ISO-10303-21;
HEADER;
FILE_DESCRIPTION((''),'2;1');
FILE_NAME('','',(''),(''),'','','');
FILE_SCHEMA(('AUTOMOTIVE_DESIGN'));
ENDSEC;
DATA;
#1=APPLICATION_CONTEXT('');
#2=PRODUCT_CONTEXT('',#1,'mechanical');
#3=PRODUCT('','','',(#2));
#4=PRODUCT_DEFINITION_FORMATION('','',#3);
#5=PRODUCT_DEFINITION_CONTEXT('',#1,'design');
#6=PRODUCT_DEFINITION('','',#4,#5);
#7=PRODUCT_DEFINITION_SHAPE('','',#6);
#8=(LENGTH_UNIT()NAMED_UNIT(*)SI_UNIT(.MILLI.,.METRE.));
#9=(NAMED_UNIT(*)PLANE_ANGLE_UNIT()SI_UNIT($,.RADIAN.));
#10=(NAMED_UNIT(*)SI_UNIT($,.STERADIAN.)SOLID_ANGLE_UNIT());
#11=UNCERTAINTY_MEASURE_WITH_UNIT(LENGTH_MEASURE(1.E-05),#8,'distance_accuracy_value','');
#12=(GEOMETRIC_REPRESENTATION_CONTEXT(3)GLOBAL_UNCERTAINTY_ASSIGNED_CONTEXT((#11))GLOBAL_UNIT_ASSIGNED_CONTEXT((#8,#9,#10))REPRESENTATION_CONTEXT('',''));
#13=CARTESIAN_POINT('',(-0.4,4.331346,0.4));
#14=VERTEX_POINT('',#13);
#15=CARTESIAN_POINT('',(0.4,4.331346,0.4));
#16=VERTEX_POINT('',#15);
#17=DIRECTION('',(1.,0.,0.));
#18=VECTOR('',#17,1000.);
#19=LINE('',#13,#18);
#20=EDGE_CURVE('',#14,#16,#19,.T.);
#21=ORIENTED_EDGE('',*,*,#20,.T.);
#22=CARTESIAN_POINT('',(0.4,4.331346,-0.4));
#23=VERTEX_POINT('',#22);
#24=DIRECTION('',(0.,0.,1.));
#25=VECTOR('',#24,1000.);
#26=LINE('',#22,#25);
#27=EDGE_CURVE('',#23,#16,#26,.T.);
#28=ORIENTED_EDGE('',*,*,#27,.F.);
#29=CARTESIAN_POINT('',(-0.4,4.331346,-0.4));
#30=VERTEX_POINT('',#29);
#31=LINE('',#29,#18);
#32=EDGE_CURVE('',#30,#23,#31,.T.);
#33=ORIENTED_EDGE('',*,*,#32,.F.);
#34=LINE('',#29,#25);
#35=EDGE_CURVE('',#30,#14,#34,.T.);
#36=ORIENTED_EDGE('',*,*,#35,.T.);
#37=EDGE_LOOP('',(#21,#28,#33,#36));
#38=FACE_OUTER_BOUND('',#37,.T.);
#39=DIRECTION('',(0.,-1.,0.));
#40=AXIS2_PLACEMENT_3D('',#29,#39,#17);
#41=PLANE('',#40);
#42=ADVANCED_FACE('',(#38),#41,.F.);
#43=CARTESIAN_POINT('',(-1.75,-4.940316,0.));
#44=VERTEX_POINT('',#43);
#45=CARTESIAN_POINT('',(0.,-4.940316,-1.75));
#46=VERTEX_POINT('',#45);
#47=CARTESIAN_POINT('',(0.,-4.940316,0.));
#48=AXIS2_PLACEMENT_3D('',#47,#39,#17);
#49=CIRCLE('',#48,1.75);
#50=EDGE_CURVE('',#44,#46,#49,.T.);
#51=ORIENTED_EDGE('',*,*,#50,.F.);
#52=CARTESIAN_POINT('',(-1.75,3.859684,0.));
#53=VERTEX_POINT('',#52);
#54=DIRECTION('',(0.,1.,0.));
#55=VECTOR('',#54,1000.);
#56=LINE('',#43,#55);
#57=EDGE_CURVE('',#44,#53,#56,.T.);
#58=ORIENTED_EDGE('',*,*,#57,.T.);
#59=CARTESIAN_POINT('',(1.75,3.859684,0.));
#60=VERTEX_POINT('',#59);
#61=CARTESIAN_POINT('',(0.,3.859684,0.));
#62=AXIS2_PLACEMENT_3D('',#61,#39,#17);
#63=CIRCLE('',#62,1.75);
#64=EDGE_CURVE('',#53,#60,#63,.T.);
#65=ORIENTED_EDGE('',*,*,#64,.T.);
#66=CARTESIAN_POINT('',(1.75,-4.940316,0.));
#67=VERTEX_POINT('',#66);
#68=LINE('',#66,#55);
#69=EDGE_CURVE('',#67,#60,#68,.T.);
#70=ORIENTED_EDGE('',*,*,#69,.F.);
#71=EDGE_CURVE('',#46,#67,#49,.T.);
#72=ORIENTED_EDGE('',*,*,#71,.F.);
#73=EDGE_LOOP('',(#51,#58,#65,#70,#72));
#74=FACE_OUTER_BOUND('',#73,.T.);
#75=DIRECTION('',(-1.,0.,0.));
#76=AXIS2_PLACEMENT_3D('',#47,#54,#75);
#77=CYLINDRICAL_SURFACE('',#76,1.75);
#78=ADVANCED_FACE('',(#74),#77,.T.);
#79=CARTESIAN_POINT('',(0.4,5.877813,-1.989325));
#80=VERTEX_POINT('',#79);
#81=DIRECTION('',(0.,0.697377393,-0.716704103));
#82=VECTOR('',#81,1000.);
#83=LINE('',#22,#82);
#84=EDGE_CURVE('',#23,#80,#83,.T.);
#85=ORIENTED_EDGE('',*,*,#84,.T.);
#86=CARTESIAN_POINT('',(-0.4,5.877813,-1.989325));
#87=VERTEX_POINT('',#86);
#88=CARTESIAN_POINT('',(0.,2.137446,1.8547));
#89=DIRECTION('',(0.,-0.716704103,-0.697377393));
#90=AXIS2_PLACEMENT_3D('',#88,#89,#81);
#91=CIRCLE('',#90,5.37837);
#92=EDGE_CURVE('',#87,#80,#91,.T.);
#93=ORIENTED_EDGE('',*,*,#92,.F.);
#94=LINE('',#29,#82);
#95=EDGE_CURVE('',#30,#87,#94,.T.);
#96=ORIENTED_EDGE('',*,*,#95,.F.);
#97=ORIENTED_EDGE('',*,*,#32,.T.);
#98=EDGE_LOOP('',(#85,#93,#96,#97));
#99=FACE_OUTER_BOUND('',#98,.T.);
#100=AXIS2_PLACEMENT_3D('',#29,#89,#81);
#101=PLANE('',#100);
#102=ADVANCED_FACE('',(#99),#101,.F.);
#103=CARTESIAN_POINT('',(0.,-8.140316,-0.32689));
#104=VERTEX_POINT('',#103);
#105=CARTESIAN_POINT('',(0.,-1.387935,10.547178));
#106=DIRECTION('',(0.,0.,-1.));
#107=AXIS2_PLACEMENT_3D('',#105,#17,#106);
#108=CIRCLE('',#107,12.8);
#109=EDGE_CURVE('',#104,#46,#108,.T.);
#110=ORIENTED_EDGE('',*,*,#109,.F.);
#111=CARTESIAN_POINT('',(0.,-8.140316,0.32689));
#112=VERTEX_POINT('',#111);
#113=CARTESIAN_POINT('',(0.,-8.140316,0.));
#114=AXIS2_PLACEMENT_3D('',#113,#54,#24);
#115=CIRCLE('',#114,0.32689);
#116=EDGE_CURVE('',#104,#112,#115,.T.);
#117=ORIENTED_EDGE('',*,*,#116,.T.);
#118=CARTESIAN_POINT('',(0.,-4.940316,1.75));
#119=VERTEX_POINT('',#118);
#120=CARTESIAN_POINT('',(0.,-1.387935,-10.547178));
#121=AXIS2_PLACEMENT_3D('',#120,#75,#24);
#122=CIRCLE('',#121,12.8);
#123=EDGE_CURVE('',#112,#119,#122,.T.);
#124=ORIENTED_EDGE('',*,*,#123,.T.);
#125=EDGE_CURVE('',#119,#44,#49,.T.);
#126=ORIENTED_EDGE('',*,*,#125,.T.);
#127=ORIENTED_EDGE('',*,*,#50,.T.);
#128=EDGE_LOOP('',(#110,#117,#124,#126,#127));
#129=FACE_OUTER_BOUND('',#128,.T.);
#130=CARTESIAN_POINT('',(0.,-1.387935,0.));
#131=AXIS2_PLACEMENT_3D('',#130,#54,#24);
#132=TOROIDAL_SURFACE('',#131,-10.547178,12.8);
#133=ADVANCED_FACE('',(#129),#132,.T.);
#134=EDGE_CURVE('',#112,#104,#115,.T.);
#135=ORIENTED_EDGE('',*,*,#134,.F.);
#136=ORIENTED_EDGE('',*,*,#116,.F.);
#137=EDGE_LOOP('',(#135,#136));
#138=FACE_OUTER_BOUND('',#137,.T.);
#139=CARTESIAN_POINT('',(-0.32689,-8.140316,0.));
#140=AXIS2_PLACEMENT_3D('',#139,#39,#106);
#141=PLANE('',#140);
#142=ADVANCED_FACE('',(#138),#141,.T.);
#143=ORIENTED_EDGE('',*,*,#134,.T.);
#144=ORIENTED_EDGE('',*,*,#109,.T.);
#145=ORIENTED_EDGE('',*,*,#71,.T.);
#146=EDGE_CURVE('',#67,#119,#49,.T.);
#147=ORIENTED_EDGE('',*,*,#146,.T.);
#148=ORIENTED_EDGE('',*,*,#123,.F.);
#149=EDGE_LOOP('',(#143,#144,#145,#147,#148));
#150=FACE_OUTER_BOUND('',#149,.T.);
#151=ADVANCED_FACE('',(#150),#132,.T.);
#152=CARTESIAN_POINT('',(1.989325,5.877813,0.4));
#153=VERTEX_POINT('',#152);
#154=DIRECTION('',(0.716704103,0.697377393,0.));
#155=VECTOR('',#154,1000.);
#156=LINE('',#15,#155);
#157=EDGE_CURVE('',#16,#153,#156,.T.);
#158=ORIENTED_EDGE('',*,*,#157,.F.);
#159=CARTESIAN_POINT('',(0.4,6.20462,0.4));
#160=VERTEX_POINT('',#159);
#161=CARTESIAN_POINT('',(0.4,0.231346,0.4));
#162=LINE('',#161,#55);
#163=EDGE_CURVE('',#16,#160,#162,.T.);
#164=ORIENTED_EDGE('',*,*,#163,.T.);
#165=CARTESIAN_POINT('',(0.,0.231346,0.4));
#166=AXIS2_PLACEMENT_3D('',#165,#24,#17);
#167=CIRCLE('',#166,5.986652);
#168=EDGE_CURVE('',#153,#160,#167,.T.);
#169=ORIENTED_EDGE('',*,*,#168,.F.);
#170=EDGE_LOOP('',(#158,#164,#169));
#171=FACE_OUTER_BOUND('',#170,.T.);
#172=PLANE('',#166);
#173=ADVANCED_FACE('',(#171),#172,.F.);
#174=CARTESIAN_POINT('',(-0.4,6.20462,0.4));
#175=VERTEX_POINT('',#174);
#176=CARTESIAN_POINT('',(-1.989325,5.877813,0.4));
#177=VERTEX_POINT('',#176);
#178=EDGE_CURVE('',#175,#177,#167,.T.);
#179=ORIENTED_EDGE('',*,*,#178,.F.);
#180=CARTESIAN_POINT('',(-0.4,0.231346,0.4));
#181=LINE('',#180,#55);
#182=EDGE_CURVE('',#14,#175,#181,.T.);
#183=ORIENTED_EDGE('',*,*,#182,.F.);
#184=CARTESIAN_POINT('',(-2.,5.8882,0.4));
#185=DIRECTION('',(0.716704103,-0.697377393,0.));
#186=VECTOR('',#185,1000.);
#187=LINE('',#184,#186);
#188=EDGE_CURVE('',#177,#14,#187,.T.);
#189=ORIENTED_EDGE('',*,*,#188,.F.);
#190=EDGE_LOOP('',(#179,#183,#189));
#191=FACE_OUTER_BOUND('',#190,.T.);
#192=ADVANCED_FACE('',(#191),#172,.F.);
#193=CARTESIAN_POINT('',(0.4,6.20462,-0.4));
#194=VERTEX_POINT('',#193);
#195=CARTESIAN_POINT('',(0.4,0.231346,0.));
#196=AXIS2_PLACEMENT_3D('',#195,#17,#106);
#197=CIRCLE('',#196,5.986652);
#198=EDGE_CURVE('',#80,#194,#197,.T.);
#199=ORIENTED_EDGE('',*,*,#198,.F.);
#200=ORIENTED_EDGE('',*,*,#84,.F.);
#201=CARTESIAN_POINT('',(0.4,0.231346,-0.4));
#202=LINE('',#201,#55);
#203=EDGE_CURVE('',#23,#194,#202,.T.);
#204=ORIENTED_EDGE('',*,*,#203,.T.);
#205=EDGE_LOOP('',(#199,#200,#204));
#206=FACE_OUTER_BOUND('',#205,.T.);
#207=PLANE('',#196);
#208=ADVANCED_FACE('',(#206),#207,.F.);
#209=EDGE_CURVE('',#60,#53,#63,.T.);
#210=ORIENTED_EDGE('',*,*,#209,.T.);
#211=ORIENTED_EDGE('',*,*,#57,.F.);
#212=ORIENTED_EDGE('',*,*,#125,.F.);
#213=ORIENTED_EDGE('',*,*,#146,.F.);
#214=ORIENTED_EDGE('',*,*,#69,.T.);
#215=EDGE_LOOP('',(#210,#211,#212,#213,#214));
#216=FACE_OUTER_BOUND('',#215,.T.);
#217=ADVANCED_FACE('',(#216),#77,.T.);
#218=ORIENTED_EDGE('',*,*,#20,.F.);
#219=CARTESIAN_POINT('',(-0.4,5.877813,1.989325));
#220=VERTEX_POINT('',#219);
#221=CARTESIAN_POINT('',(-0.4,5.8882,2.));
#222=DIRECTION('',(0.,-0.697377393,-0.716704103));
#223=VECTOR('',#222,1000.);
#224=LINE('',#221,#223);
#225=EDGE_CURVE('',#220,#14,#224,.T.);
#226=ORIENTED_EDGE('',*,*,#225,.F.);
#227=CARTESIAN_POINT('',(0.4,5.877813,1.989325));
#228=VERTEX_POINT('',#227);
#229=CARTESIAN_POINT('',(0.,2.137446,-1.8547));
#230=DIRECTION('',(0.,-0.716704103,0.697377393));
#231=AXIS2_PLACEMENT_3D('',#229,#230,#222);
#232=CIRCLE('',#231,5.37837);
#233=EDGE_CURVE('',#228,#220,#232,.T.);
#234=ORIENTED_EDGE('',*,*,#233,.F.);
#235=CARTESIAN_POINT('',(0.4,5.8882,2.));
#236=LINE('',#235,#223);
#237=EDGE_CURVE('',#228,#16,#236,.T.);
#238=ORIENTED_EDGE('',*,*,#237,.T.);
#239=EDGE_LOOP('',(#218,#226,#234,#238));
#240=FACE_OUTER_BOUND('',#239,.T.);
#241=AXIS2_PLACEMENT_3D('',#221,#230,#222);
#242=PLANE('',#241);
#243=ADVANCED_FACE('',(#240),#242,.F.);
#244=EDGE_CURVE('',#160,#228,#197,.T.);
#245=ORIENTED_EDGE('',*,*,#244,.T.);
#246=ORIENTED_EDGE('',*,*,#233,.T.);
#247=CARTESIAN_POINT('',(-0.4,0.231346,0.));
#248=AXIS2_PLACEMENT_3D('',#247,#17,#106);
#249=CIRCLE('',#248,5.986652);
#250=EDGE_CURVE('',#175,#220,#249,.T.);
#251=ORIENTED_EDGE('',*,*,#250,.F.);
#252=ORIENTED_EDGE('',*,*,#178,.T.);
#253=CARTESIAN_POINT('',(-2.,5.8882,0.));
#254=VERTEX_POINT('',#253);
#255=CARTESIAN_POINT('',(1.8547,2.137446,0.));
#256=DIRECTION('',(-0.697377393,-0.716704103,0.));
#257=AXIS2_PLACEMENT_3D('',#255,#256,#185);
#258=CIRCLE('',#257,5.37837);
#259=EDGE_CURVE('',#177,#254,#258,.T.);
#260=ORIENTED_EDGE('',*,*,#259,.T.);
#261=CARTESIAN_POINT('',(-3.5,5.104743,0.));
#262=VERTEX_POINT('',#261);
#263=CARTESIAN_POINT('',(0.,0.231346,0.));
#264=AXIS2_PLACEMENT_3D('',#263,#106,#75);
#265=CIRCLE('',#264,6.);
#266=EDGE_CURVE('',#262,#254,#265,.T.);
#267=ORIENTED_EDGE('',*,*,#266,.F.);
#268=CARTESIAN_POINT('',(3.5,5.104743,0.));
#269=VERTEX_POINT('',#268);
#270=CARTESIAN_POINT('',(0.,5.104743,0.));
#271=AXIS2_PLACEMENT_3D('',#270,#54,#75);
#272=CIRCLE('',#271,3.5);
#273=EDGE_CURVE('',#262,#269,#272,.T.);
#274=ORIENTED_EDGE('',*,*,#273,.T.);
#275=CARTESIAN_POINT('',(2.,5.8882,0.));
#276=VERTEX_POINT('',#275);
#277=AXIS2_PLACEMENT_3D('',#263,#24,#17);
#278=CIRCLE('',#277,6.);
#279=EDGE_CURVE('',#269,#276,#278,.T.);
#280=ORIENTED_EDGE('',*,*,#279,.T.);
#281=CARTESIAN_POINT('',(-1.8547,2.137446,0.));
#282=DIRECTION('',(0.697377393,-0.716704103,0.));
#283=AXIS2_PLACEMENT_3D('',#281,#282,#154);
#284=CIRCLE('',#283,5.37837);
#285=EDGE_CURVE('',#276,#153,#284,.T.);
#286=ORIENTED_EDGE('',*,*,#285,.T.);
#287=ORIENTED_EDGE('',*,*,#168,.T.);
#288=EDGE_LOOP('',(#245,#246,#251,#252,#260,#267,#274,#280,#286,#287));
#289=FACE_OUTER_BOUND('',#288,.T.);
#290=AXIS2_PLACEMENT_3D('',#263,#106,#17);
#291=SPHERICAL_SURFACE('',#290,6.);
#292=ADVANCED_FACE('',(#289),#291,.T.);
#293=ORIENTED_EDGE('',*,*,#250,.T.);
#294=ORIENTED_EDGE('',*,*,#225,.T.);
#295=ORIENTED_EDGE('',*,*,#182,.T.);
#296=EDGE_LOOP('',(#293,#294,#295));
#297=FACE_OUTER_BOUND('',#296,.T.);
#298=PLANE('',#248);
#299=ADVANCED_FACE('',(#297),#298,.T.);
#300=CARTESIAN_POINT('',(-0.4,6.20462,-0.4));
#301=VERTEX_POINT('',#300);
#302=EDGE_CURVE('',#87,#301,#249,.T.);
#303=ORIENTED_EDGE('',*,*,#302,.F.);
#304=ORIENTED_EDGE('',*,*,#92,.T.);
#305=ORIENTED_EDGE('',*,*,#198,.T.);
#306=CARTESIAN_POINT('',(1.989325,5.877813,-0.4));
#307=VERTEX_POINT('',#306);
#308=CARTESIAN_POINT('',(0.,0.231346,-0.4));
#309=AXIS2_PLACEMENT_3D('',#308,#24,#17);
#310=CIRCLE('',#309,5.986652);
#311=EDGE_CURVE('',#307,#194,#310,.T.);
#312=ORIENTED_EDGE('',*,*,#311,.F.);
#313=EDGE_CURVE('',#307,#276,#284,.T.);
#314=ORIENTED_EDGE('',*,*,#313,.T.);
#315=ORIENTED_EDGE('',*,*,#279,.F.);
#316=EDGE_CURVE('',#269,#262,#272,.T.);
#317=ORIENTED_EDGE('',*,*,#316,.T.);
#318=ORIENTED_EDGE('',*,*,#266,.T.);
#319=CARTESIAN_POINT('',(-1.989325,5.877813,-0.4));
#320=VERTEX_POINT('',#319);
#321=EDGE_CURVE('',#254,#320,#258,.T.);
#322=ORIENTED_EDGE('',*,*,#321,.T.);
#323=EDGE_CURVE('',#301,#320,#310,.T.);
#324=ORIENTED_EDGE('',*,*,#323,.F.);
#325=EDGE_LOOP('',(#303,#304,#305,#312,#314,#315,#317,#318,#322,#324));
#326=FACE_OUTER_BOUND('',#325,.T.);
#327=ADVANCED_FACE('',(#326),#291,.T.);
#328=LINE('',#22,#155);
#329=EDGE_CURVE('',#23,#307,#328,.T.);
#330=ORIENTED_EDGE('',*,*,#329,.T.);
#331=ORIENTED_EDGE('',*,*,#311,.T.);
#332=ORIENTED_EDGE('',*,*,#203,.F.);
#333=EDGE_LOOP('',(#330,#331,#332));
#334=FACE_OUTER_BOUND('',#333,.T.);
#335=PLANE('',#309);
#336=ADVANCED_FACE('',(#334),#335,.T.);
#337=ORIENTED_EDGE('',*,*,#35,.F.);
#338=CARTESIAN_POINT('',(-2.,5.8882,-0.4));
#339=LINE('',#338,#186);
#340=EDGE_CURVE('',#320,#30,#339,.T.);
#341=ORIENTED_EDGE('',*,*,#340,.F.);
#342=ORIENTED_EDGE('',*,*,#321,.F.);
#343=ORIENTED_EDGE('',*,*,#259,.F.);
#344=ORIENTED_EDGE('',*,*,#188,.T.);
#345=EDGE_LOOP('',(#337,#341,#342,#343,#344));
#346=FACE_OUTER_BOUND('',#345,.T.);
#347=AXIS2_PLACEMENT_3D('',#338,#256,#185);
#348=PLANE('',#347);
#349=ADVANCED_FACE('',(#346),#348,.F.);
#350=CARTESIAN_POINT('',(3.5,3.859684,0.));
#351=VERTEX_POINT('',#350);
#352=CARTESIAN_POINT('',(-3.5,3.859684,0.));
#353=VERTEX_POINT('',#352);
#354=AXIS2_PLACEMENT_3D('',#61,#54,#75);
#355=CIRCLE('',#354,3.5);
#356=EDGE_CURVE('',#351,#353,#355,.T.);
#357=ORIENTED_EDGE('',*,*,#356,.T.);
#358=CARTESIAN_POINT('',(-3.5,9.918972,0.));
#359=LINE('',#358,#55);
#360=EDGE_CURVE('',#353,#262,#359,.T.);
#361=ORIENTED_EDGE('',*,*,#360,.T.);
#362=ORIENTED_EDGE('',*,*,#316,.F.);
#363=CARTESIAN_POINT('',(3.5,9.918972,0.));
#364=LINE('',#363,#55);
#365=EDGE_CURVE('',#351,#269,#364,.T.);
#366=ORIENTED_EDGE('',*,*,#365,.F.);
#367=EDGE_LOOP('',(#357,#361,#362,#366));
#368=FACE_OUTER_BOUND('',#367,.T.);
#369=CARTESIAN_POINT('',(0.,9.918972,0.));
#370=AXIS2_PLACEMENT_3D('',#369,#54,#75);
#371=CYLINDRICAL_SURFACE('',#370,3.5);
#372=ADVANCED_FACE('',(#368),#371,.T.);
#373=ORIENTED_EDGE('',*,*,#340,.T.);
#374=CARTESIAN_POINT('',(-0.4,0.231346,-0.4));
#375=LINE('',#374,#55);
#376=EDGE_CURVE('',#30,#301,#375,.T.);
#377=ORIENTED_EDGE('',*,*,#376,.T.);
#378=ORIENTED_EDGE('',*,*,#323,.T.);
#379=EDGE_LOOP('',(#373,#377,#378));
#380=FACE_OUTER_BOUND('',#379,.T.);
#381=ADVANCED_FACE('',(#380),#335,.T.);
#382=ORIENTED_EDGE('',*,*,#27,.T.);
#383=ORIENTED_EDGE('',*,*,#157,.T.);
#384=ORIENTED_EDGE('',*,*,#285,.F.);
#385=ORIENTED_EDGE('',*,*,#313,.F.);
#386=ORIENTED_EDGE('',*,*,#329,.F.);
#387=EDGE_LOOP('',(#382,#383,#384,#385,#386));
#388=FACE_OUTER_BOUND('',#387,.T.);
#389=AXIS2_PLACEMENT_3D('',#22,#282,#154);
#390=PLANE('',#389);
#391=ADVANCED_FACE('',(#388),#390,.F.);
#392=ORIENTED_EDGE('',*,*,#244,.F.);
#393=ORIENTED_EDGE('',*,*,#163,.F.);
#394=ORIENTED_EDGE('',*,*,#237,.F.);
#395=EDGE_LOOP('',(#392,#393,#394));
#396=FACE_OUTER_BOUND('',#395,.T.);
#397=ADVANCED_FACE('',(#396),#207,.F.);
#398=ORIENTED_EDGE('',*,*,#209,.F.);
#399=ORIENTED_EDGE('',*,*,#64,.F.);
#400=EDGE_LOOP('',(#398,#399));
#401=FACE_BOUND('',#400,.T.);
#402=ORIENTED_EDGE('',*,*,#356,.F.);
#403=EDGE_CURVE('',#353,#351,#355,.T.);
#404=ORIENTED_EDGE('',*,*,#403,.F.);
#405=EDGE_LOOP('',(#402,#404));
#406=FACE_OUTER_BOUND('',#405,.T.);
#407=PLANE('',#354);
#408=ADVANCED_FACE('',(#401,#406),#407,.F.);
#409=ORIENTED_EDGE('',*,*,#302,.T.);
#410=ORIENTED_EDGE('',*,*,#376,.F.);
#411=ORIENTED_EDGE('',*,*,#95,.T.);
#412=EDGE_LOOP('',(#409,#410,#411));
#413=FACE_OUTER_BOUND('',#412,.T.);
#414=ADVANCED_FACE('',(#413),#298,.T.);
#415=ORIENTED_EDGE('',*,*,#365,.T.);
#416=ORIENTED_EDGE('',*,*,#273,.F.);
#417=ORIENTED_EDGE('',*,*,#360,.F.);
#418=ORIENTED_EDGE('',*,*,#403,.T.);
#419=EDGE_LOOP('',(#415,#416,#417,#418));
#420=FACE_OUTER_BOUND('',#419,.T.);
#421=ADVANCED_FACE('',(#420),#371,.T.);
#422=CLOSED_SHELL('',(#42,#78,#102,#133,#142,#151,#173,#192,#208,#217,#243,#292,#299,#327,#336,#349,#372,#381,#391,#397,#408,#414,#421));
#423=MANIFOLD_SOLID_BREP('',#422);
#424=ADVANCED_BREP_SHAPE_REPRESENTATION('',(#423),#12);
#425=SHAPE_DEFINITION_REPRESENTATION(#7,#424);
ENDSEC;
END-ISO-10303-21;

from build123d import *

# Parameters (mm, degrees)
SKETCH2_R           = 1.75
BOSS_EXTRUDE1_DEPTH = 8.8
CUT_EXTRUDE1_DEPTH  = 0.4
CIRPATTERN1_COUNT   = 4


with BuildPart() as part:
    # Sketch1 → Revolve2 (revolve)
    with BuildSketch(Plane.XY, mode=Mode.PRIVATE) as revolve2_sk:
        with BuildLine():
            Line((0, 3.8596837944664038), (3.5000000000000013, 3.8596837944664038))
            Line((3.5000000000000013, 3.8596837944664038), (3.5000000000000013, 5.104743083003953))
            ThreePointArc((3.5000000000000013, 5.104743083003953), (1.8384255445316686, 5.9427548013385545), (8.7e-16, 6.231345910599472))
            Line((8.7e-16, 6.231345910599472), (0, 3.8596837944664038))
        make_face()
    revolve(revolve2_sk.sketch.rotate(Axis((0, 9.918972332015809, 0), (2.4e-16, -1, 0)), 180), axis=Axis((0, 9.918972332015809, 0), (2.4e-16, -1, 0)))

    # Sketch2 → Boss-Extrude1 (add)
    with BuildSketch(Plane.XZ.offset(-3.8596837944664033)):
        Circle(SKETCH2_R)
    extrude(amount=BOSS_EXTRUDE1_DEPTH)

    # Sketch3 → Revolve3 (revolve)
    with BuildSketch(Plane.XY, mode=Mode.PRIVATE) as revolve3_sk:
        with BuildLine():
            Line((-0.3268895580285352, -8.140316205533598), (0, -8.140316205533598))
            Line((0, -8.140316205533598), (-3.69e-15, -4.940316205533597))
            Line((-3.69e-15, -4.940316205533597), (-1.7500000000000084, -4.940316205533597))
            ThreePointArc((-1.7500000000000084, -4.940316205533597), (-1.148404721070234, -6.5892178123268526), (-0.3268895580285352, -8.140316205533598))
        make_face()
    revolve(revolve3_sk.sketch.rotate(Axis((0, 0, 0), (0, -1, 0)), 180), axis=Axis((0, 0, 0), (0, -1, 0)))

    # Sketch8 → Cut-Extrude1 (cut, symmetric)
    with BuildSketch(Plane.XY):
        with BuildLine():
            Line((-2, 5.888200160091848), (-0.3999999999999996, 4.331345910599471))
            Line((-0.3999999999999996, 4.331345910599471), (0.40000000000000047, 4.33134591059947))
            Line((0.40000000000000047, 4.33134591059947), (2, 5.8882001600918485))
            ThreePointArc((2, 5.8882001600918485), (3.4e-16, 6.231345910599467), (-2, 5.888200160091848))
        make_face()
    cut_extrude1 = extrude(amount=CUT_EXTRUDE1_DEPTH, both=True, mode=Mode.SUBTRACT)

    # CirPattern1: Cut-Extrude1 ×4 about axis
    cirpattern1_axis = Axis((3.1e-16, 0, 3.1e-16), (0, 1, 0))
    for i in range(1, CIRPATTERN1_COUNT):
        add(cut_extrude1.rotate(cirpattern1_axis, i * 360 / CIRPATTERN1_COUNT), mode=Mode.SUBTRACT)


solid = part.part
